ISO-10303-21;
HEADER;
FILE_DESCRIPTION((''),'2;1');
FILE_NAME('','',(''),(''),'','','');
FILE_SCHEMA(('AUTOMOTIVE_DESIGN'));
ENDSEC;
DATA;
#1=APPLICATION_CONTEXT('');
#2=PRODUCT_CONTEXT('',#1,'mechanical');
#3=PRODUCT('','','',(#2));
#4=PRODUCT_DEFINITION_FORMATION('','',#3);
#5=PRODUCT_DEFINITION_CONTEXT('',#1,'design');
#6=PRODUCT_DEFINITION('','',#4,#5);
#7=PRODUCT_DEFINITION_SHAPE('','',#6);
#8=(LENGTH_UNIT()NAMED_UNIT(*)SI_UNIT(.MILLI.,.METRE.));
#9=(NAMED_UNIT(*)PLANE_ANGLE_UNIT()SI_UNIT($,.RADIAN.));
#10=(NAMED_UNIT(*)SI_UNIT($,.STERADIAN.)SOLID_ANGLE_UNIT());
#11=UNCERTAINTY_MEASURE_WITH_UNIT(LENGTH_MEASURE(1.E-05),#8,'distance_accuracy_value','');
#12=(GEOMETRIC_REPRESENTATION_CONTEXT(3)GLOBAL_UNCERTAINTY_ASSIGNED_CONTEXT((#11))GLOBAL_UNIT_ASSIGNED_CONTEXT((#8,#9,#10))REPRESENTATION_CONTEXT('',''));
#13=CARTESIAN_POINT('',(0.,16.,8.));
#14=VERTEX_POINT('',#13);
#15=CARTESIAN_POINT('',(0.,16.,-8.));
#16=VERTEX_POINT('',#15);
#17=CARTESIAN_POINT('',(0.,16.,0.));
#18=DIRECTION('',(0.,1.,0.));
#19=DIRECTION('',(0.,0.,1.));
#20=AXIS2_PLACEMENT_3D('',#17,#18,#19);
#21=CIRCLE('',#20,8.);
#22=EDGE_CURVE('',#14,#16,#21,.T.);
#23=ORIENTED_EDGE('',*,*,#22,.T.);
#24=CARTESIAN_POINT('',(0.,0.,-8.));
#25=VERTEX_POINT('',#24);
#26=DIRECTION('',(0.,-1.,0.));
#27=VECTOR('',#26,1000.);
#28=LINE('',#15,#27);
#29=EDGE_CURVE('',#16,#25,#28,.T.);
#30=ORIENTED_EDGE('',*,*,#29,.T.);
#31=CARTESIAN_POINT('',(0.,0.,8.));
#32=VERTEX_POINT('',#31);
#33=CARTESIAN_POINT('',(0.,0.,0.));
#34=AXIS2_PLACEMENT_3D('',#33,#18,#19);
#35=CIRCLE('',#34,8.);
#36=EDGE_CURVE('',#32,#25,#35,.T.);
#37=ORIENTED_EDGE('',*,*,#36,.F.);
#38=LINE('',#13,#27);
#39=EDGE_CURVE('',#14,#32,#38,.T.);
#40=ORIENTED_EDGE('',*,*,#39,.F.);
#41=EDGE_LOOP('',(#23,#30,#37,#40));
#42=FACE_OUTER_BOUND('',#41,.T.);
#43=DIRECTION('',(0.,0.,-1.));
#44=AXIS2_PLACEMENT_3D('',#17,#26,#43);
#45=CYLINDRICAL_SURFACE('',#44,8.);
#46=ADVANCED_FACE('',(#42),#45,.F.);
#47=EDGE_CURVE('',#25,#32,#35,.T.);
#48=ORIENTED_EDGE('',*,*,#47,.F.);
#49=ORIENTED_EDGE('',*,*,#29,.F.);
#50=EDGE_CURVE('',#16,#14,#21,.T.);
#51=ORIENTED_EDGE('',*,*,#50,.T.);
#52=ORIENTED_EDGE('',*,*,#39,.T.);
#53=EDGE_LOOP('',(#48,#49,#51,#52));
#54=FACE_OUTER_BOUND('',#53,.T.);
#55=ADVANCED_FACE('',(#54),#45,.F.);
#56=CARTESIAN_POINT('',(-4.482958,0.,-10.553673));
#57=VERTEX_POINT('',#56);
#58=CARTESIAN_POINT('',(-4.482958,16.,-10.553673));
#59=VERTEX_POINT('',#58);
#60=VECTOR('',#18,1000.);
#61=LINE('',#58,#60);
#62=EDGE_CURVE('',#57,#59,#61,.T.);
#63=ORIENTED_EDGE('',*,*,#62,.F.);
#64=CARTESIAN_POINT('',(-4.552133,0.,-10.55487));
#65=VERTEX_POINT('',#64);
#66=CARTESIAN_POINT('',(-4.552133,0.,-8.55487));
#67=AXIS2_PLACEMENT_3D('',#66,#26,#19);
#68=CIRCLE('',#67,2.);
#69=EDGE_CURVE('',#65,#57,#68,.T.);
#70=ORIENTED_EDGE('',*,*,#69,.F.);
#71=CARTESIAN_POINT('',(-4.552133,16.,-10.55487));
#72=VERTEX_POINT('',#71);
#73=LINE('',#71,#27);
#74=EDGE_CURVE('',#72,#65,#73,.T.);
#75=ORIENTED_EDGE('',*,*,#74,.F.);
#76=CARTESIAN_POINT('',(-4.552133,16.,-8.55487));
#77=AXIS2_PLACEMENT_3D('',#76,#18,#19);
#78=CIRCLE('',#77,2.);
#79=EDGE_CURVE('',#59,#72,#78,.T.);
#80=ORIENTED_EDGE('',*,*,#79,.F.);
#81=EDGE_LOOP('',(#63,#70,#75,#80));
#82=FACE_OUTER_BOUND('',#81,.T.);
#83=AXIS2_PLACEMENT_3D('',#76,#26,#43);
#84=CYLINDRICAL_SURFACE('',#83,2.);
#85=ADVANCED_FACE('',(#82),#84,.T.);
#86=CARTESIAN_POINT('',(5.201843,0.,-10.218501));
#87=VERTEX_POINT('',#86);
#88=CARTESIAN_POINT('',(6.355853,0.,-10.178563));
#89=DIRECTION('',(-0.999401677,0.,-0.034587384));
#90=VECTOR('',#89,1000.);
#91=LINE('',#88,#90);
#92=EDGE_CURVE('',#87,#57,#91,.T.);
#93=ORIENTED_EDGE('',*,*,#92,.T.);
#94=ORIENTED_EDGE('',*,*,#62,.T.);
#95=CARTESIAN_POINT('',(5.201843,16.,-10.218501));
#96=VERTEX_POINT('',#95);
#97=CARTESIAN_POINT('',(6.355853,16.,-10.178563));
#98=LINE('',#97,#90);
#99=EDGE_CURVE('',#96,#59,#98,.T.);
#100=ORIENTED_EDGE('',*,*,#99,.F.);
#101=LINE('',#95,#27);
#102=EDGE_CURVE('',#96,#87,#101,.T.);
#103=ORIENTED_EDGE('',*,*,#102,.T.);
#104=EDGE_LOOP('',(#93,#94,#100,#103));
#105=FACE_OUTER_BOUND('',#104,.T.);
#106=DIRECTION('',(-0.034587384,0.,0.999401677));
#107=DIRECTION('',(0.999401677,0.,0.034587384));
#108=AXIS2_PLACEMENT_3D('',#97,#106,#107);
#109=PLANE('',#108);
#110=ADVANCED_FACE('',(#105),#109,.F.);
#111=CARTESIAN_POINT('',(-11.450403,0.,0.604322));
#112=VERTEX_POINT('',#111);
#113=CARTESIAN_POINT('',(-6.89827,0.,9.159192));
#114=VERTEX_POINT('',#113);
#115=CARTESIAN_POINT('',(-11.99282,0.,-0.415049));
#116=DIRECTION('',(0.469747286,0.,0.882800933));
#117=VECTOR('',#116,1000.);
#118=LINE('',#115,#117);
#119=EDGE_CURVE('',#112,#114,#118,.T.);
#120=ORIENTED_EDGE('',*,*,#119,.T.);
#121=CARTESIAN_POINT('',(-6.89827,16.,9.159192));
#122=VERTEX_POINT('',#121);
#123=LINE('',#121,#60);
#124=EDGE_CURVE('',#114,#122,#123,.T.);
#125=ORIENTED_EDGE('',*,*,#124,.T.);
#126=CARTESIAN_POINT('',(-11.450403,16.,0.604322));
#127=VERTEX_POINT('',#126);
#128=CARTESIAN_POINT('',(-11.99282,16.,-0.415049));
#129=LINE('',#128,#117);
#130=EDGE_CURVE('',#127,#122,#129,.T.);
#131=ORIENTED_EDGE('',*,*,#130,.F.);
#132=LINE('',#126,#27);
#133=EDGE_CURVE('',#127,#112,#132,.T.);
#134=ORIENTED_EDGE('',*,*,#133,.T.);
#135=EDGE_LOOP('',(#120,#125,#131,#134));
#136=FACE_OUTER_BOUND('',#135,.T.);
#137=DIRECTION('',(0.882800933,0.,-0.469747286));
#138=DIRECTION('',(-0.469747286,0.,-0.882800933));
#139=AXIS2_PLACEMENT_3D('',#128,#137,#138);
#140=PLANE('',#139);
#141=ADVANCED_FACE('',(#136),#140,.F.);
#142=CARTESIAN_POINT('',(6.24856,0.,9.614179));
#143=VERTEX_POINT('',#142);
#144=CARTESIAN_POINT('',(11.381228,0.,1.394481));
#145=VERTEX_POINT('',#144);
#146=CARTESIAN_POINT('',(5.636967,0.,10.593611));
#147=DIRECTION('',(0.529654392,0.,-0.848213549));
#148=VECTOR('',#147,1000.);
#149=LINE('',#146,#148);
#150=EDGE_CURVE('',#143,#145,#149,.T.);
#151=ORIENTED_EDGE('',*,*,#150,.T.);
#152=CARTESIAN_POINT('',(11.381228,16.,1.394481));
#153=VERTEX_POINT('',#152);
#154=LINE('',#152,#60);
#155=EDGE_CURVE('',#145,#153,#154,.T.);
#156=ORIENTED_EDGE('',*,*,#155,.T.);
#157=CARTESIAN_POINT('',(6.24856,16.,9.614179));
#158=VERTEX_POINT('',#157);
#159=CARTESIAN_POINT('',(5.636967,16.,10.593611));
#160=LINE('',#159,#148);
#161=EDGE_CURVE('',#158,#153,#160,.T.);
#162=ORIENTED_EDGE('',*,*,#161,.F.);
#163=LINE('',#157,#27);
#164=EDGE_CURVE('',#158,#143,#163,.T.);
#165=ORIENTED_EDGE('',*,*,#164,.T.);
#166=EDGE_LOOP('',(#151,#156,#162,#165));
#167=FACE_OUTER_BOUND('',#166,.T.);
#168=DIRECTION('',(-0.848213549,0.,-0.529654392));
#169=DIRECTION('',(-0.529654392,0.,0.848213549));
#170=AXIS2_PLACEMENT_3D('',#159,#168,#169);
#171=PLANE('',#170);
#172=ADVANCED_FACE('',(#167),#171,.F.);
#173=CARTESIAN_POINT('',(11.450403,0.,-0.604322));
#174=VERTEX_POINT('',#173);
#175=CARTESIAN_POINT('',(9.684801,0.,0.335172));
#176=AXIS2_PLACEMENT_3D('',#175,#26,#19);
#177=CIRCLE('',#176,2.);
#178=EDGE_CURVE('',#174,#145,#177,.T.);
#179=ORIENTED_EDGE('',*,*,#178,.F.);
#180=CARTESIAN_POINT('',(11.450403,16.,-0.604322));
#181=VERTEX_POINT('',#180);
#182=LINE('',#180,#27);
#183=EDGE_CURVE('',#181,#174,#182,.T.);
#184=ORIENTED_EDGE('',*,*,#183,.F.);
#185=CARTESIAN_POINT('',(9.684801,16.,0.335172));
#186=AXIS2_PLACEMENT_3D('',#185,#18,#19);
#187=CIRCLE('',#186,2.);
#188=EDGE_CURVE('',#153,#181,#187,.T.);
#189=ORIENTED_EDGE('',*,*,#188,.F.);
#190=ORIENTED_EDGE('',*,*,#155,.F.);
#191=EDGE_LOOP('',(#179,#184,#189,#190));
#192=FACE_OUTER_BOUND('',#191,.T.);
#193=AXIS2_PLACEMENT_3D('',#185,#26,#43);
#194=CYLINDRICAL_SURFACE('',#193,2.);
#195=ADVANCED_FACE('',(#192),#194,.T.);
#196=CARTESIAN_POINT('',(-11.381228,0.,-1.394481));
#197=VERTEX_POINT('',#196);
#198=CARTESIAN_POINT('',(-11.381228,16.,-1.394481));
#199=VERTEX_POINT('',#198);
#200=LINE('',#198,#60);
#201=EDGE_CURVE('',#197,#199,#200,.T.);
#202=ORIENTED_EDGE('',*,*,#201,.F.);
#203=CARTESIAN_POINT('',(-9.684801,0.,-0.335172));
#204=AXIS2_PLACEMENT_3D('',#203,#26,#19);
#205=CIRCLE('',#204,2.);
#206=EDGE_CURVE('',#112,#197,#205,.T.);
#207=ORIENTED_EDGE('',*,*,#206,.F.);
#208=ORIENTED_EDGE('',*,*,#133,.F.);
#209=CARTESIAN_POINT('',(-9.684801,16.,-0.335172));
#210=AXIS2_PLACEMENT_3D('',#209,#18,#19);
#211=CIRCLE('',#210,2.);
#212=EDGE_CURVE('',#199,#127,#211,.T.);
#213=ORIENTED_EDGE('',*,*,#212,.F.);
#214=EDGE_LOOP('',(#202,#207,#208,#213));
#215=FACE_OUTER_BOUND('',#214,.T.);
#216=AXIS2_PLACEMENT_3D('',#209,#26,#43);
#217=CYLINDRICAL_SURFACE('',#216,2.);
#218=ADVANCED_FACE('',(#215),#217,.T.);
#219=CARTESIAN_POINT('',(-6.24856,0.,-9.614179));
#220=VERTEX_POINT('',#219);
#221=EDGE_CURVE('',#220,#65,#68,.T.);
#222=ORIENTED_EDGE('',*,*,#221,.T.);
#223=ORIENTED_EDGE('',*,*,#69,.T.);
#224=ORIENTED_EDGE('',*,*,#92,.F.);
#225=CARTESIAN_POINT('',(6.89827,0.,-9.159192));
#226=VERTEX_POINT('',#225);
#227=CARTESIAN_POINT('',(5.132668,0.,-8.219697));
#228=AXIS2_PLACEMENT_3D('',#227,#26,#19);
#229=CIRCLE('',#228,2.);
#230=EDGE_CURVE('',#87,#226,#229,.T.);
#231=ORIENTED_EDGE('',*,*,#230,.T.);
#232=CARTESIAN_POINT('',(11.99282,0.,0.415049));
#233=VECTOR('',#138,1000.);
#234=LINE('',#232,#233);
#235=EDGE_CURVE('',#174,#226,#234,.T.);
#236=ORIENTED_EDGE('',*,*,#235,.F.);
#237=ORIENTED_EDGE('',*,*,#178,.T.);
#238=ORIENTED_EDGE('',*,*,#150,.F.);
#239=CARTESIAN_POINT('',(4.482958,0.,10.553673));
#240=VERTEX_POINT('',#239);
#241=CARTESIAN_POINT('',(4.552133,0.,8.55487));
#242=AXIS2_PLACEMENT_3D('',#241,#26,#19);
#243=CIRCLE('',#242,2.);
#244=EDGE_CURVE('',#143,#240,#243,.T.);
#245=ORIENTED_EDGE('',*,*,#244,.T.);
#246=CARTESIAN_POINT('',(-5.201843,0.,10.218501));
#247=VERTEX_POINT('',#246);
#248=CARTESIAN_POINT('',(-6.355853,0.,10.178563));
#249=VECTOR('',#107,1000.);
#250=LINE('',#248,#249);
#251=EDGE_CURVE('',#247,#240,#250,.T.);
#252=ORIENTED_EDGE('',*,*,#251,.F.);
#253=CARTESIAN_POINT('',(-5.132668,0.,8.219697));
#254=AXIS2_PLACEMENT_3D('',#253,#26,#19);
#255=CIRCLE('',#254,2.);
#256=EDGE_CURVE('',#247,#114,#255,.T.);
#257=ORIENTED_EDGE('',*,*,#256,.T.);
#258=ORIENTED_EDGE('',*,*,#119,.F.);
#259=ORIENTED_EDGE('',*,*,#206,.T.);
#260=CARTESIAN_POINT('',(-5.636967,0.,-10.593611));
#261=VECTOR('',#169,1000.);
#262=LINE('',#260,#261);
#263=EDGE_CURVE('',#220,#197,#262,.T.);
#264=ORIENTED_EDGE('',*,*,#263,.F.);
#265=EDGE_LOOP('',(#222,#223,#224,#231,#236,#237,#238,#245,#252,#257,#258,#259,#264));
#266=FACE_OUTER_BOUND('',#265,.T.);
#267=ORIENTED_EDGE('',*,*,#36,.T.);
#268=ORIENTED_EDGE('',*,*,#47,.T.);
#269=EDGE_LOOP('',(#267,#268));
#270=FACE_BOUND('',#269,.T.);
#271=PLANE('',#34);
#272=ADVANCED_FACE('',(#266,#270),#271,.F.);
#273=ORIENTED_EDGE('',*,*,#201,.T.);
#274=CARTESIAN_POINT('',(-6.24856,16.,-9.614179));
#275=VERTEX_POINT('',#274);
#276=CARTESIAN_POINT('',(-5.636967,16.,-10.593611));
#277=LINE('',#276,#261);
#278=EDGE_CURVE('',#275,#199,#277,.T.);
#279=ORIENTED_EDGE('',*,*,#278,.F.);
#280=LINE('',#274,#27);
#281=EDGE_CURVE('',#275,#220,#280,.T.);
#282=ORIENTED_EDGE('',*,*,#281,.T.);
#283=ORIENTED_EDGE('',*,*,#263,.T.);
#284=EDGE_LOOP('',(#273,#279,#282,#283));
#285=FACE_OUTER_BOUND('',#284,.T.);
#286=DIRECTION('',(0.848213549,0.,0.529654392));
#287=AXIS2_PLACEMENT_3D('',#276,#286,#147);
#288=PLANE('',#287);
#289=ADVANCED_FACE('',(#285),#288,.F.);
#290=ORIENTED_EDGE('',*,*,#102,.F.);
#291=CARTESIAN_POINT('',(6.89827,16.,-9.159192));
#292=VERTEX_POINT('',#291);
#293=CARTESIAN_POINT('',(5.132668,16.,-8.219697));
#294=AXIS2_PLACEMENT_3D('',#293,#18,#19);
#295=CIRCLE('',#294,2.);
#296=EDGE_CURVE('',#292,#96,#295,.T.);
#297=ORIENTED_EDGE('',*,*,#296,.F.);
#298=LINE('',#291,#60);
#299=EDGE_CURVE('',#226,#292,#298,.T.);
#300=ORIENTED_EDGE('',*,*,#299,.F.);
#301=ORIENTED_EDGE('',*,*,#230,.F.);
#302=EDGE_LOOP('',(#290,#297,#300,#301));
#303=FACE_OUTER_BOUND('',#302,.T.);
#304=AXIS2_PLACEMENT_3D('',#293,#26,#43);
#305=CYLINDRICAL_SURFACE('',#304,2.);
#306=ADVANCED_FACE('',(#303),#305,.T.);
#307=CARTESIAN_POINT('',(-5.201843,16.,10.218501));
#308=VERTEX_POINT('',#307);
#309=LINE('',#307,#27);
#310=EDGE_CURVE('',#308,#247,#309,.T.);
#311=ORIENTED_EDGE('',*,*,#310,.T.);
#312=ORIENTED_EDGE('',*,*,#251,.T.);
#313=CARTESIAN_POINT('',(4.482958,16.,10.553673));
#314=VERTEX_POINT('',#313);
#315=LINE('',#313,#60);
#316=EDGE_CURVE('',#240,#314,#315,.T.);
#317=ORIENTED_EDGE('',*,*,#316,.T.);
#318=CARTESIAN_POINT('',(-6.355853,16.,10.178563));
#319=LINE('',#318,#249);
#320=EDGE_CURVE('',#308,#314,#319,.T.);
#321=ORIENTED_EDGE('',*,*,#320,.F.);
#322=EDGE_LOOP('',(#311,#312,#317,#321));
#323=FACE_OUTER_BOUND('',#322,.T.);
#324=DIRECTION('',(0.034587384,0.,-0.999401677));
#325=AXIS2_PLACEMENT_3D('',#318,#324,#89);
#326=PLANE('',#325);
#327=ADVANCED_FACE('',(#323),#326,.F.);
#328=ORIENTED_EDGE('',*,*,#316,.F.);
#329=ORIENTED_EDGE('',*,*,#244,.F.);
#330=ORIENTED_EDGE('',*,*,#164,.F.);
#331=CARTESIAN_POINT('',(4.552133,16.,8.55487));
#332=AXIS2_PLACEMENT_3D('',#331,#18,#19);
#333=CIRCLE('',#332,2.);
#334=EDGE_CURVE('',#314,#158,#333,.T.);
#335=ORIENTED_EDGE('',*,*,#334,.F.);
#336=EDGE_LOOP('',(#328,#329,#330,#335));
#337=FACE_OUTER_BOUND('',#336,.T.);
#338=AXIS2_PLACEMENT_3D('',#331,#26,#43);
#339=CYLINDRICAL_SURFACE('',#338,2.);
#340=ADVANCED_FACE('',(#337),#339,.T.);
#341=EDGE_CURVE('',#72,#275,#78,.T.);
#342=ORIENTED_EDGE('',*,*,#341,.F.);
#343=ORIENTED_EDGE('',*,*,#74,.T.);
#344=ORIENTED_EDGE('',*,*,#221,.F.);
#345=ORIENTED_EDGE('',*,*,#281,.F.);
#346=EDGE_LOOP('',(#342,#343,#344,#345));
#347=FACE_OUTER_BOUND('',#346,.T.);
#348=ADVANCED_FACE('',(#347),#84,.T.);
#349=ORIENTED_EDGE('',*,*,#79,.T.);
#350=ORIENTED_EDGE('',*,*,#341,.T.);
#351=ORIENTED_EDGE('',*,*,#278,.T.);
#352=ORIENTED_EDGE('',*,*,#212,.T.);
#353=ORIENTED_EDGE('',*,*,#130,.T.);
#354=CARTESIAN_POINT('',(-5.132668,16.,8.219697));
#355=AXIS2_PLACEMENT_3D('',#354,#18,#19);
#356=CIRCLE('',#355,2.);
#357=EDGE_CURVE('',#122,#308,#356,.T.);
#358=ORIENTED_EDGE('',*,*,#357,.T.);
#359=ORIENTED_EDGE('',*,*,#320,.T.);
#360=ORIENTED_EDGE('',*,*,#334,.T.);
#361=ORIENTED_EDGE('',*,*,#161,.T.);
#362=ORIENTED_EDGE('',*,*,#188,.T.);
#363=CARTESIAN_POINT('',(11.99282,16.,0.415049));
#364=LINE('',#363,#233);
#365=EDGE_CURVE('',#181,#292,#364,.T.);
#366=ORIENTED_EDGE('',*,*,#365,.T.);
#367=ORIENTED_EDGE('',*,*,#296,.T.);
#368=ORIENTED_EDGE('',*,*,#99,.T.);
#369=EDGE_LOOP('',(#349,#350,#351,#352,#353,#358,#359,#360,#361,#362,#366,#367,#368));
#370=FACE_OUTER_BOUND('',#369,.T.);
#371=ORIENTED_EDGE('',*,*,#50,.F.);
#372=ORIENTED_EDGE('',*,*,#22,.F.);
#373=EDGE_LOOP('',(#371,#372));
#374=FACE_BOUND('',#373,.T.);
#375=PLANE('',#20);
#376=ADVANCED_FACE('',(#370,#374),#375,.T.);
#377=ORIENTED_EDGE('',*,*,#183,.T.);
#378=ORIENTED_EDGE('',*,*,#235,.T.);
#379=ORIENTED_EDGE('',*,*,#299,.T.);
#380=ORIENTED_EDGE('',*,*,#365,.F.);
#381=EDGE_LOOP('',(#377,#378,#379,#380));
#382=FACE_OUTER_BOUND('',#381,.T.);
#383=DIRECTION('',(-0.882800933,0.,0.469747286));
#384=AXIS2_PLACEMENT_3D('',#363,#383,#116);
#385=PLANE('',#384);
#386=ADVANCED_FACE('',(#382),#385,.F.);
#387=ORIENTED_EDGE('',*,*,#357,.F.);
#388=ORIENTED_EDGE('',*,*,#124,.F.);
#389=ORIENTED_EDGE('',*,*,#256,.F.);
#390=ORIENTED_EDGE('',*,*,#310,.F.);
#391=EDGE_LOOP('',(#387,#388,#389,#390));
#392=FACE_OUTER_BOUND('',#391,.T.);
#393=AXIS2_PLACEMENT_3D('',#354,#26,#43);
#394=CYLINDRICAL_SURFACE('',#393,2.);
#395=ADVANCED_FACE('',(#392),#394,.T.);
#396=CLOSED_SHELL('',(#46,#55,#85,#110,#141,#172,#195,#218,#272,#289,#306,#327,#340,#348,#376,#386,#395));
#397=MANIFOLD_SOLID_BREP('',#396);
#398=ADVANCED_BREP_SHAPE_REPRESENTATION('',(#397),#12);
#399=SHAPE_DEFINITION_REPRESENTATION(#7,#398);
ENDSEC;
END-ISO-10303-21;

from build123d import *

# Parameters (mm, degrees)
SKETCH1_R           = 8
BOSS_EXTRUDE1_DEPTH = 16
FILLET1_R           = 2
FILLET2_R           = 2


with BuildPart() as part:
    # Sketch1 → Boss-Extrude1 (new body)
    with BuildSketch(Plane(origin=(0, 0, 0), x_dir=(1, 0, 0), z_dir=(0, 1, 0))):
        Polygon((5.636967427, -10.593611199), (11.992820129, -0.415048607), (6.355852702, 10.178562591), (-5.636967427, 10.593611199), (-11.992820129, 0.415048607), (-6.355852702, -10.178562591), align=None)
        with Locations(Location((0, 0, 0), (0, 0, 270))):
            Circle(SKETCH1_R, mode=Mode.SUBTRACT)
    extrude(amount=BOSS_EXTRUDE1_DEPTH)

    # Fillet1
    fillet1_edges = [part.edges().sort_by_distance(p)[0] for p in [
        (5.636967427, 8, 10.593611199),
    ]]
    fillet(fillet1_edges, radius=FILLET1_R)

    # Fillet2
    fillet2_edges = [part.edges().sort_by_distance(p)[0] for p in [
        (-6.355852702, 8, 10.178562591),
        (-11.992820129, 8, -0.415048607),
        (-5.636967427, 8, -10.593611199),
        (6.355852702, 8, -10.178562591),
        (11.992820129, 8, 0.415048607),
    ]]
    fillet(fillet2_edges, radius=FILLET2_R)


solid = part.part
